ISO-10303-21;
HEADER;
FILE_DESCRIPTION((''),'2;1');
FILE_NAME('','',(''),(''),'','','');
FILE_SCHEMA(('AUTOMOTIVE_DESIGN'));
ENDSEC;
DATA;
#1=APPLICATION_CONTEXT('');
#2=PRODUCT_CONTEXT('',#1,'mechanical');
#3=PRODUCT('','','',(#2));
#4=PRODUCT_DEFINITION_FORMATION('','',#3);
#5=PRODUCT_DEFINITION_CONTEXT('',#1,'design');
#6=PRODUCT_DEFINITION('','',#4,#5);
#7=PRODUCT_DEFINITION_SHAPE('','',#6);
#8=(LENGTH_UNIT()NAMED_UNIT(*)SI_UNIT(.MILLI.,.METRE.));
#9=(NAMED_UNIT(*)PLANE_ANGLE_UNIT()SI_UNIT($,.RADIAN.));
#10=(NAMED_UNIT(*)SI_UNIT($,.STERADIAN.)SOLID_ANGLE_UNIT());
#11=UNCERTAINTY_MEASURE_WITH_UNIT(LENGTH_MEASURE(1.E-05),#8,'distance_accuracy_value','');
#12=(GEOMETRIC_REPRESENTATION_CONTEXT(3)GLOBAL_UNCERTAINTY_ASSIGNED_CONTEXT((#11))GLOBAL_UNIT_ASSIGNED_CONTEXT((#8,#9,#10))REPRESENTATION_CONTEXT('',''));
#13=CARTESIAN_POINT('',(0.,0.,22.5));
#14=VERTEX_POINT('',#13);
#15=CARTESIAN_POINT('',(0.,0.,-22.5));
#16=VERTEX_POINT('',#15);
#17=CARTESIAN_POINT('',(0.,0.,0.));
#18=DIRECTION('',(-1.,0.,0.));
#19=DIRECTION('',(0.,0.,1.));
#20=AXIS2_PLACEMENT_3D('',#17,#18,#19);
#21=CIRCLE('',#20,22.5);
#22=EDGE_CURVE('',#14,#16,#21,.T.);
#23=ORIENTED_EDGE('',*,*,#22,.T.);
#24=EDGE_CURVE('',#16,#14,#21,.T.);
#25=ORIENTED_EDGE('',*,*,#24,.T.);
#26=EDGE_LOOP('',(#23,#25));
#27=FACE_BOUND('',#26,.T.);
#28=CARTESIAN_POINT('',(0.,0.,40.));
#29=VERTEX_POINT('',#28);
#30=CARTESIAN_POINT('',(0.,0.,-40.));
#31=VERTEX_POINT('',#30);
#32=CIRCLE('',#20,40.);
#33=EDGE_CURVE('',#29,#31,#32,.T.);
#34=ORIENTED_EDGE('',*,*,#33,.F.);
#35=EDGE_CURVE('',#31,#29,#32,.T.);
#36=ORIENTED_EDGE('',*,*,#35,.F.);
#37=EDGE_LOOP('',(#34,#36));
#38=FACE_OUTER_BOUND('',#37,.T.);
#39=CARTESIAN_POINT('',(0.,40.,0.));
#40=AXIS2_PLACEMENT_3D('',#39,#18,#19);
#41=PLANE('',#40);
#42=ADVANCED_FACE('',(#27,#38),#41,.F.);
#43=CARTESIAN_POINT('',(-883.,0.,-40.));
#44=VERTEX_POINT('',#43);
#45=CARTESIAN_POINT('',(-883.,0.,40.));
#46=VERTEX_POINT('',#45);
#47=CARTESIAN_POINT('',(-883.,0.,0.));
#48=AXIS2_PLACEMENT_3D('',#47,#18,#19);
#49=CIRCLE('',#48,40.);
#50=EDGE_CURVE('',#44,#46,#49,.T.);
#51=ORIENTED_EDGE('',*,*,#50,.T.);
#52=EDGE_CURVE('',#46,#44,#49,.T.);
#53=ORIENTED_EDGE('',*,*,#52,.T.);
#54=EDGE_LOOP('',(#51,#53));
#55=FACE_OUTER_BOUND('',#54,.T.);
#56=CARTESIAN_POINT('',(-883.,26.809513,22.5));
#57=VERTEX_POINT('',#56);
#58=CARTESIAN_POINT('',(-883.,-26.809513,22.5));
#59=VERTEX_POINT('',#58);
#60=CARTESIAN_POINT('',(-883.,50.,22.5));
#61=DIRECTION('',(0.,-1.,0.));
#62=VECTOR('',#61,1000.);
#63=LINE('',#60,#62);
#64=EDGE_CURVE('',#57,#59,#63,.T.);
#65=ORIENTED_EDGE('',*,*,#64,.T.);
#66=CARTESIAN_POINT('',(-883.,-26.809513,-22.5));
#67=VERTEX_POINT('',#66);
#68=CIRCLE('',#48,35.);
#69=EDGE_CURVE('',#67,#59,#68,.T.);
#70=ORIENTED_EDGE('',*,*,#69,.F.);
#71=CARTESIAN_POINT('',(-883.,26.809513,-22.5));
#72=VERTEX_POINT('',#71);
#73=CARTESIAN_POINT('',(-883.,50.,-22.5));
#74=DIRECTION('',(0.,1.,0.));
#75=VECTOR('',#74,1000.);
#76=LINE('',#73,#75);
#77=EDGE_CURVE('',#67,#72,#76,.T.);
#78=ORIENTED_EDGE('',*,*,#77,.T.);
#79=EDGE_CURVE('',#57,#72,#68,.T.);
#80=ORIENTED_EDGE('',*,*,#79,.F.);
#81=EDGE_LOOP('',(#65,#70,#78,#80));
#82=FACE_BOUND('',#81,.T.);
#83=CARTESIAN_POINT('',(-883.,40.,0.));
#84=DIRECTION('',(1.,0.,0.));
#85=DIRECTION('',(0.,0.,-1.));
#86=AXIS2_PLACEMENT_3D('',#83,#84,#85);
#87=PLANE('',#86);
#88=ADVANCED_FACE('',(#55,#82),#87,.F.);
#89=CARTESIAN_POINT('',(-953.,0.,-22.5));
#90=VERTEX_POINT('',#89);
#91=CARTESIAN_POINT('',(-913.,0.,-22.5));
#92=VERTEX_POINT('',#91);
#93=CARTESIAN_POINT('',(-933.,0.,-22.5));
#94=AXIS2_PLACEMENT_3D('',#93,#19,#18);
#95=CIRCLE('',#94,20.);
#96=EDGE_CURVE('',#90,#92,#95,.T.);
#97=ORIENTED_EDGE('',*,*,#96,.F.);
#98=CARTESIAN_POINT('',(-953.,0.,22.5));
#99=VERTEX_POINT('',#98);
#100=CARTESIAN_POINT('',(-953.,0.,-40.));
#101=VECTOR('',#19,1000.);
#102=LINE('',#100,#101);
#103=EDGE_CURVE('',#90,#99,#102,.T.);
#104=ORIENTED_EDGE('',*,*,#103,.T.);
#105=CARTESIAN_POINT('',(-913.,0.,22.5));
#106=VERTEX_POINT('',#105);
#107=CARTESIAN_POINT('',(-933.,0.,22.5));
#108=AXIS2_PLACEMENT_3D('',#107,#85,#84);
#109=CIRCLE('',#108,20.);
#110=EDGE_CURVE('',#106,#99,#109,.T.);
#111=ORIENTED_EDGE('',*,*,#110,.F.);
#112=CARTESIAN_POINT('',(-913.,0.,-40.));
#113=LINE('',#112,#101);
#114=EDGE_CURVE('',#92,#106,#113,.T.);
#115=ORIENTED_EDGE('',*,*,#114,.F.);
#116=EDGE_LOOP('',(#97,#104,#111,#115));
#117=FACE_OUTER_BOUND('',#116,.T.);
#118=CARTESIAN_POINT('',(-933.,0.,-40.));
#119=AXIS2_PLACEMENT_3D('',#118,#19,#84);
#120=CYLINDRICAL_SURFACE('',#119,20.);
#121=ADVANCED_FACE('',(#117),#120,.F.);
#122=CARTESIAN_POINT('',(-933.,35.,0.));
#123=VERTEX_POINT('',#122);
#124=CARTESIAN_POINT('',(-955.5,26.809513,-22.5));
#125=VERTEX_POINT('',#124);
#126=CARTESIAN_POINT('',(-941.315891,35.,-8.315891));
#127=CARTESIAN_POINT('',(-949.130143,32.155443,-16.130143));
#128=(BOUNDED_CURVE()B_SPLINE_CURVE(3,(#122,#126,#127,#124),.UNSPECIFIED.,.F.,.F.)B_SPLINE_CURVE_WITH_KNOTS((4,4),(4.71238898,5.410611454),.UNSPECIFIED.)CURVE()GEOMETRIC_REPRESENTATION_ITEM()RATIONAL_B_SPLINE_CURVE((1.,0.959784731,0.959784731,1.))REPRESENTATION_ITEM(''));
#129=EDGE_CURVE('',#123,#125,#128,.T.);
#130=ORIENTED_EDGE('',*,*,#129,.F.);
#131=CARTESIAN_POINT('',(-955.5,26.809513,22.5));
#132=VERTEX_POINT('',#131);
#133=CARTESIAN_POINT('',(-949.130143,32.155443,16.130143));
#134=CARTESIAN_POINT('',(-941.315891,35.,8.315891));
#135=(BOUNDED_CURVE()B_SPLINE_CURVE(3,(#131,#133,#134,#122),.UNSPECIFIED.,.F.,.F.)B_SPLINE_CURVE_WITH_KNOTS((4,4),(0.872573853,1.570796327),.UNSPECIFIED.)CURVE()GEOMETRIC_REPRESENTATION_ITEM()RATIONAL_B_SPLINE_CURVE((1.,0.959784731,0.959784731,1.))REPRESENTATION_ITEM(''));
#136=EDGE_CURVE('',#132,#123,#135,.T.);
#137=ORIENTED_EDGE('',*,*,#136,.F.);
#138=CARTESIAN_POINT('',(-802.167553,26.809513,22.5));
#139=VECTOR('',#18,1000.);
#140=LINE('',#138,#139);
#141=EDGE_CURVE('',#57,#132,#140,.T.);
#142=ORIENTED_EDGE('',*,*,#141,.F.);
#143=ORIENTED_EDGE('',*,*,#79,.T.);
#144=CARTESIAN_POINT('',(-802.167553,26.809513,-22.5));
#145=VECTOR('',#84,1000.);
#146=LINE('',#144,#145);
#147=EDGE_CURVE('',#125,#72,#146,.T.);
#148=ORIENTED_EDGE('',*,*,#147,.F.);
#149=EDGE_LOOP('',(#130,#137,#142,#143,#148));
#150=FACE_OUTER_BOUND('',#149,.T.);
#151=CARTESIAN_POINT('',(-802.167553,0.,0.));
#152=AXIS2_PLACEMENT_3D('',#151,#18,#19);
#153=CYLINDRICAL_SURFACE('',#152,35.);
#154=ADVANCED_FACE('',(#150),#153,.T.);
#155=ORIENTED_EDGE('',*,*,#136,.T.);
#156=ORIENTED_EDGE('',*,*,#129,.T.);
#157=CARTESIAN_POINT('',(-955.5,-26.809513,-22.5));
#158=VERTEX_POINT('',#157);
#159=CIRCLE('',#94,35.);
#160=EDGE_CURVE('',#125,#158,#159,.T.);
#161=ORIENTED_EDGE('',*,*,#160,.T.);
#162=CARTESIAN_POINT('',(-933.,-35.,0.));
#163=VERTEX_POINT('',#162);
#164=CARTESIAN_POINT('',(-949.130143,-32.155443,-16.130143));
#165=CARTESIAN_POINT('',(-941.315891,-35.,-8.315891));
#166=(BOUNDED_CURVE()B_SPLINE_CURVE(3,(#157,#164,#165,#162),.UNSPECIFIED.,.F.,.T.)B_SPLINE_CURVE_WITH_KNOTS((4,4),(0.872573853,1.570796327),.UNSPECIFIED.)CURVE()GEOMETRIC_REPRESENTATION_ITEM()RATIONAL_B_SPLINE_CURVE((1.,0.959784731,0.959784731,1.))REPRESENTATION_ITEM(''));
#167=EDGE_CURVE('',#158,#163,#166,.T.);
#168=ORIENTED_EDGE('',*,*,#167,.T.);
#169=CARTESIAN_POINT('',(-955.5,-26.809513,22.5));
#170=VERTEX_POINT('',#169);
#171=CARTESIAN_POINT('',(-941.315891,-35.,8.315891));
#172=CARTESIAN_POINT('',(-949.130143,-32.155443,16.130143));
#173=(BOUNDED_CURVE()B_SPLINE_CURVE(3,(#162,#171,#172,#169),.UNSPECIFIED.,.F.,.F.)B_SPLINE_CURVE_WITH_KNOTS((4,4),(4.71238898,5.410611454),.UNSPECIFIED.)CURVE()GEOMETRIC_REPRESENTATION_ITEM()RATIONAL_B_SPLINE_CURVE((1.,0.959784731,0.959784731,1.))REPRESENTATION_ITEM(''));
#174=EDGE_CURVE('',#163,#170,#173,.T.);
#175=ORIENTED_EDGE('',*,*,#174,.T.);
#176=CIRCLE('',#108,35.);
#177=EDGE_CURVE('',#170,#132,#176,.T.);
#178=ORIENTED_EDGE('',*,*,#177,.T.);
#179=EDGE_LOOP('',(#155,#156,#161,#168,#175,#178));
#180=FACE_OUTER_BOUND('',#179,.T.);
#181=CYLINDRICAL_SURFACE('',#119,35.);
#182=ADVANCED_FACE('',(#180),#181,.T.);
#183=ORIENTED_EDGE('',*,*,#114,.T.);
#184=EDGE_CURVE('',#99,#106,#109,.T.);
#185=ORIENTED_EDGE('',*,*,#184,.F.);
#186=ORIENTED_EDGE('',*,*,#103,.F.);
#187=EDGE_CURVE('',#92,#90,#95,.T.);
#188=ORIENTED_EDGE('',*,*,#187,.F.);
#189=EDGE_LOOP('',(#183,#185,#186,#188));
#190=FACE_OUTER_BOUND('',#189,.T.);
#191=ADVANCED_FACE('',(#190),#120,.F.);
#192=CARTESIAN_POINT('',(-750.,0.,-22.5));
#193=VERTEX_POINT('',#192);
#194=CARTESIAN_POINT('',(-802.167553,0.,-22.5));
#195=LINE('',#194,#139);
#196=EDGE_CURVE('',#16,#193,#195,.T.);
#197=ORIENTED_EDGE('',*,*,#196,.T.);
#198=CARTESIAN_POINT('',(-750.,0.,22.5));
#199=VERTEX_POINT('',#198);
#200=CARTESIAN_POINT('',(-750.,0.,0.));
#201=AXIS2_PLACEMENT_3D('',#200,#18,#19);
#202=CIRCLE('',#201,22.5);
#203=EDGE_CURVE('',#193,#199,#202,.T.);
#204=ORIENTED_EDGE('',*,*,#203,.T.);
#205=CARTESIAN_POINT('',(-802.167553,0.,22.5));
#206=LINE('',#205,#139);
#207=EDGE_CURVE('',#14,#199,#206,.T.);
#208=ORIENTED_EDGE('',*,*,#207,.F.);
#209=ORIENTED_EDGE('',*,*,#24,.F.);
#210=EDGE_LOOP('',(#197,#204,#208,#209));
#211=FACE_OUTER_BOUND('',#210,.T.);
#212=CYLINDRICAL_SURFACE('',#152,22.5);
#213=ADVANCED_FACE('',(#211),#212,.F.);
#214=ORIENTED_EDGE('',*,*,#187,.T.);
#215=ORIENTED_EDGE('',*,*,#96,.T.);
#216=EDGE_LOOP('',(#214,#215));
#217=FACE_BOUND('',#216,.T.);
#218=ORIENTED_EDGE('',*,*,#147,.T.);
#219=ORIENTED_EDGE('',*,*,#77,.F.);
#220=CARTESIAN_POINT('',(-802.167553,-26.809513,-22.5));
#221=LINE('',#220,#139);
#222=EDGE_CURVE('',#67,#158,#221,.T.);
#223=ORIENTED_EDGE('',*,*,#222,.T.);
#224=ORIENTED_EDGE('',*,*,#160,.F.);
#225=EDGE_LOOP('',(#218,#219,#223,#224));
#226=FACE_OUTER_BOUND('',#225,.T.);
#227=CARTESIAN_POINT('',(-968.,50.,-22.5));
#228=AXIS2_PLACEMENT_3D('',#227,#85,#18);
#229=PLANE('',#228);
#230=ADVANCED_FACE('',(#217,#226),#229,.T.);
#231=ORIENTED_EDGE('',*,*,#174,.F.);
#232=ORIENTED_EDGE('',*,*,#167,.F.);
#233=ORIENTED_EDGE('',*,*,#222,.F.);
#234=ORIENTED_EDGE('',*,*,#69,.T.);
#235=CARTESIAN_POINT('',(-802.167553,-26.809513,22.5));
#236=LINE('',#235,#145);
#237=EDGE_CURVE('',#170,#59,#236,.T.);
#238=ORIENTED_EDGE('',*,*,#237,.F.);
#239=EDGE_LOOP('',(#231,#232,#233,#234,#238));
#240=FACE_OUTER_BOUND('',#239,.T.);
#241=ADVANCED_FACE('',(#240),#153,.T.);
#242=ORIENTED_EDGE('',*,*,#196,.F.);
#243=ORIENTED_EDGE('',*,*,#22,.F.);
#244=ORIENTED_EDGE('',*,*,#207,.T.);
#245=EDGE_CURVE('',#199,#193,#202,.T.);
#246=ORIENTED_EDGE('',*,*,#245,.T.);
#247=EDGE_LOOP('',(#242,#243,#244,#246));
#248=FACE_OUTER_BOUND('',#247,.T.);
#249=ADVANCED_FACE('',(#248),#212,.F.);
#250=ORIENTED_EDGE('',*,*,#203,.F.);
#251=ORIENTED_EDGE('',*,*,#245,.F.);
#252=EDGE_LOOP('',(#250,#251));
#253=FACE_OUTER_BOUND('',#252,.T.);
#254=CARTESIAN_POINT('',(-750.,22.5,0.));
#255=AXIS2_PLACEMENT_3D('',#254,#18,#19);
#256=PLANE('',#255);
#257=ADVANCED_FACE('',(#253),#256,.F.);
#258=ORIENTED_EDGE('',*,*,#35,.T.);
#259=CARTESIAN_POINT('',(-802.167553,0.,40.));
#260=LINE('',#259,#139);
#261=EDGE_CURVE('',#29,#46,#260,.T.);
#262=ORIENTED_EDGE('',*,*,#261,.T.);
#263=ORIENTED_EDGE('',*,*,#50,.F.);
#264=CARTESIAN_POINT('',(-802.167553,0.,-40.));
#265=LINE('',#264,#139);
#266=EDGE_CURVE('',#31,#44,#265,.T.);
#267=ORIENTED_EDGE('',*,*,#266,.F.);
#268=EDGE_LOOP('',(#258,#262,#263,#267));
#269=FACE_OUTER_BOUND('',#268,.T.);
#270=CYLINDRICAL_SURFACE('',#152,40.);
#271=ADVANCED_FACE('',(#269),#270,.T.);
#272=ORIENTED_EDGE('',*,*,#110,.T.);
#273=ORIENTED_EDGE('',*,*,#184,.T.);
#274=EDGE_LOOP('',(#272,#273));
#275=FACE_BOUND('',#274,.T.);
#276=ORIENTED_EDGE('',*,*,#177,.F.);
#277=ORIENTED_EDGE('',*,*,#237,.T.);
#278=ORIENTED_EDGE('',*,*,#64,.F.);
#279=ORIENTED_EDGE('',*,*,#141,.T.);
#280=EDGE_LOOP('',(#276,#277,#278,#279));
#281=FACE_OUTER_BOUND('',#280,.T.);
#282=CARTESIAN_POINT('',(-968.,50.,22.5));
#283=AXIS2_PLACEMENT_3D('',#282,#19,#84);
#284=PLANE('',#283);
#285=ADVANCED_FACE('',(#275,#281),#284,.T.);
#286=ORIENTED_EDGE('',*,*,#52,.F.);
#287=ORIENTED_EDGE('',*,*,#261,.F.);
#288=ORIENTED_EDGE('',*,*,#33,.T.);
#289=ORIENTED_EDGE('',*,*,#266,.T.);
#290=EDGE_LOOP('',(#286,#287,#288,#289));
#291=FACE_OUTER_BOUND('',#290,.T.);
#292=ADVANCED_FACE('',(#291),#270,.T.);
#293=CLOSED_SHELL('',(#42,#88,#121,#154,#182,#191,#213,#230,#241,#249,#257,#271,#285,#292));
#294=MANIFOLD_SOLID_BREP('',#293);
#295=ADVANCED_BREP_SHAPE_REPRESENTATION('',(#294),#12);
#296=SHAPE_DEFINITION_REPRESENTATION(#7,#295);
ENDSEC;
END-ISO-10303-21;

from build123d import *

# Parameters (mm, degrees)
CUT_EXTRUDE_1_DEPTH      = 970.651483782
CUT_EXTRUDE_1_DEPTH_BACK = 970.651483782
SKETCH_2_R               = 20
SKETCH_3_W               = 28.175076561
SKETCH_3_H               = 100
CUT_EXTRUDE_2_DEPTH      = 885.810149128


with BuildPart() as part:
    # Sketch 1 → Revolve 1 (revolve)
    with BuildSketch(Plane.XY, mode=Mode.PRIVATE) as revolve_1_sk:
        Polygon((0, 40), (-883, 40), (-883, 35), (-968, 35), (-968, 0), (-750, 0), (-750, 22.5), (0, 22.5), align=None)
    revolve(revolve_1_sk.sketch.rotate(Axis((-802.16755253, 0, 0), (1, 0, 0)), 90), axis=Axis((-802.16755253, 0, 0), (1, 0, 0)))

    # Sketch 2 → Cut-Extrude 1 (cut, two sides: drawn at the far end of the back side and taken through both)
    with BuildSketch(Plane.XY.offset(-CUT_EXTRUDE_1_DEPTH_BACK)):
        with BuildLine():
            Line((-968, 35), (-968, 0))
            ThreePointArc((-968, 0), (-957.748737342, 24.748737342), (-933, 35))
            Line((-933, 35), (-968, 35))
        make_face()
        with BuildLine():
            Line((-968, 0), (-968, -35))
            Line((-968, -35), (-933, -35))
            ThreePointArc((-933, -35), (-957.748737342, -24.748737342), (-968, 0))
        make_face()
        with Locations((-933, 0)):
            Circle(SKETCH_2_R)
    extrude(amount=CUT_EXTRUDE_1_DEPTH + CUT_EXTRUDE_1_DEPTH_BACK, mode=Mode.SUBTRACT)

    # Sketch 3 → Cut-Extrude 2 (cut, through all)
    with BuildSketch(Plane.ZY.offset(883)):
        with Locations((-36.58753828, 0)):
            Rectangle(SKETCH_3_W, SKETCH_3_H)
        with Locations((36.58753828, 0)):
            Rectangle(SKETCH_3_W, SKETCH_3_H)
    extrude(amount=CUT_EXTRUDE_2_DEPTH, mode=Mode.SUBTRACT)


solid = part.part
